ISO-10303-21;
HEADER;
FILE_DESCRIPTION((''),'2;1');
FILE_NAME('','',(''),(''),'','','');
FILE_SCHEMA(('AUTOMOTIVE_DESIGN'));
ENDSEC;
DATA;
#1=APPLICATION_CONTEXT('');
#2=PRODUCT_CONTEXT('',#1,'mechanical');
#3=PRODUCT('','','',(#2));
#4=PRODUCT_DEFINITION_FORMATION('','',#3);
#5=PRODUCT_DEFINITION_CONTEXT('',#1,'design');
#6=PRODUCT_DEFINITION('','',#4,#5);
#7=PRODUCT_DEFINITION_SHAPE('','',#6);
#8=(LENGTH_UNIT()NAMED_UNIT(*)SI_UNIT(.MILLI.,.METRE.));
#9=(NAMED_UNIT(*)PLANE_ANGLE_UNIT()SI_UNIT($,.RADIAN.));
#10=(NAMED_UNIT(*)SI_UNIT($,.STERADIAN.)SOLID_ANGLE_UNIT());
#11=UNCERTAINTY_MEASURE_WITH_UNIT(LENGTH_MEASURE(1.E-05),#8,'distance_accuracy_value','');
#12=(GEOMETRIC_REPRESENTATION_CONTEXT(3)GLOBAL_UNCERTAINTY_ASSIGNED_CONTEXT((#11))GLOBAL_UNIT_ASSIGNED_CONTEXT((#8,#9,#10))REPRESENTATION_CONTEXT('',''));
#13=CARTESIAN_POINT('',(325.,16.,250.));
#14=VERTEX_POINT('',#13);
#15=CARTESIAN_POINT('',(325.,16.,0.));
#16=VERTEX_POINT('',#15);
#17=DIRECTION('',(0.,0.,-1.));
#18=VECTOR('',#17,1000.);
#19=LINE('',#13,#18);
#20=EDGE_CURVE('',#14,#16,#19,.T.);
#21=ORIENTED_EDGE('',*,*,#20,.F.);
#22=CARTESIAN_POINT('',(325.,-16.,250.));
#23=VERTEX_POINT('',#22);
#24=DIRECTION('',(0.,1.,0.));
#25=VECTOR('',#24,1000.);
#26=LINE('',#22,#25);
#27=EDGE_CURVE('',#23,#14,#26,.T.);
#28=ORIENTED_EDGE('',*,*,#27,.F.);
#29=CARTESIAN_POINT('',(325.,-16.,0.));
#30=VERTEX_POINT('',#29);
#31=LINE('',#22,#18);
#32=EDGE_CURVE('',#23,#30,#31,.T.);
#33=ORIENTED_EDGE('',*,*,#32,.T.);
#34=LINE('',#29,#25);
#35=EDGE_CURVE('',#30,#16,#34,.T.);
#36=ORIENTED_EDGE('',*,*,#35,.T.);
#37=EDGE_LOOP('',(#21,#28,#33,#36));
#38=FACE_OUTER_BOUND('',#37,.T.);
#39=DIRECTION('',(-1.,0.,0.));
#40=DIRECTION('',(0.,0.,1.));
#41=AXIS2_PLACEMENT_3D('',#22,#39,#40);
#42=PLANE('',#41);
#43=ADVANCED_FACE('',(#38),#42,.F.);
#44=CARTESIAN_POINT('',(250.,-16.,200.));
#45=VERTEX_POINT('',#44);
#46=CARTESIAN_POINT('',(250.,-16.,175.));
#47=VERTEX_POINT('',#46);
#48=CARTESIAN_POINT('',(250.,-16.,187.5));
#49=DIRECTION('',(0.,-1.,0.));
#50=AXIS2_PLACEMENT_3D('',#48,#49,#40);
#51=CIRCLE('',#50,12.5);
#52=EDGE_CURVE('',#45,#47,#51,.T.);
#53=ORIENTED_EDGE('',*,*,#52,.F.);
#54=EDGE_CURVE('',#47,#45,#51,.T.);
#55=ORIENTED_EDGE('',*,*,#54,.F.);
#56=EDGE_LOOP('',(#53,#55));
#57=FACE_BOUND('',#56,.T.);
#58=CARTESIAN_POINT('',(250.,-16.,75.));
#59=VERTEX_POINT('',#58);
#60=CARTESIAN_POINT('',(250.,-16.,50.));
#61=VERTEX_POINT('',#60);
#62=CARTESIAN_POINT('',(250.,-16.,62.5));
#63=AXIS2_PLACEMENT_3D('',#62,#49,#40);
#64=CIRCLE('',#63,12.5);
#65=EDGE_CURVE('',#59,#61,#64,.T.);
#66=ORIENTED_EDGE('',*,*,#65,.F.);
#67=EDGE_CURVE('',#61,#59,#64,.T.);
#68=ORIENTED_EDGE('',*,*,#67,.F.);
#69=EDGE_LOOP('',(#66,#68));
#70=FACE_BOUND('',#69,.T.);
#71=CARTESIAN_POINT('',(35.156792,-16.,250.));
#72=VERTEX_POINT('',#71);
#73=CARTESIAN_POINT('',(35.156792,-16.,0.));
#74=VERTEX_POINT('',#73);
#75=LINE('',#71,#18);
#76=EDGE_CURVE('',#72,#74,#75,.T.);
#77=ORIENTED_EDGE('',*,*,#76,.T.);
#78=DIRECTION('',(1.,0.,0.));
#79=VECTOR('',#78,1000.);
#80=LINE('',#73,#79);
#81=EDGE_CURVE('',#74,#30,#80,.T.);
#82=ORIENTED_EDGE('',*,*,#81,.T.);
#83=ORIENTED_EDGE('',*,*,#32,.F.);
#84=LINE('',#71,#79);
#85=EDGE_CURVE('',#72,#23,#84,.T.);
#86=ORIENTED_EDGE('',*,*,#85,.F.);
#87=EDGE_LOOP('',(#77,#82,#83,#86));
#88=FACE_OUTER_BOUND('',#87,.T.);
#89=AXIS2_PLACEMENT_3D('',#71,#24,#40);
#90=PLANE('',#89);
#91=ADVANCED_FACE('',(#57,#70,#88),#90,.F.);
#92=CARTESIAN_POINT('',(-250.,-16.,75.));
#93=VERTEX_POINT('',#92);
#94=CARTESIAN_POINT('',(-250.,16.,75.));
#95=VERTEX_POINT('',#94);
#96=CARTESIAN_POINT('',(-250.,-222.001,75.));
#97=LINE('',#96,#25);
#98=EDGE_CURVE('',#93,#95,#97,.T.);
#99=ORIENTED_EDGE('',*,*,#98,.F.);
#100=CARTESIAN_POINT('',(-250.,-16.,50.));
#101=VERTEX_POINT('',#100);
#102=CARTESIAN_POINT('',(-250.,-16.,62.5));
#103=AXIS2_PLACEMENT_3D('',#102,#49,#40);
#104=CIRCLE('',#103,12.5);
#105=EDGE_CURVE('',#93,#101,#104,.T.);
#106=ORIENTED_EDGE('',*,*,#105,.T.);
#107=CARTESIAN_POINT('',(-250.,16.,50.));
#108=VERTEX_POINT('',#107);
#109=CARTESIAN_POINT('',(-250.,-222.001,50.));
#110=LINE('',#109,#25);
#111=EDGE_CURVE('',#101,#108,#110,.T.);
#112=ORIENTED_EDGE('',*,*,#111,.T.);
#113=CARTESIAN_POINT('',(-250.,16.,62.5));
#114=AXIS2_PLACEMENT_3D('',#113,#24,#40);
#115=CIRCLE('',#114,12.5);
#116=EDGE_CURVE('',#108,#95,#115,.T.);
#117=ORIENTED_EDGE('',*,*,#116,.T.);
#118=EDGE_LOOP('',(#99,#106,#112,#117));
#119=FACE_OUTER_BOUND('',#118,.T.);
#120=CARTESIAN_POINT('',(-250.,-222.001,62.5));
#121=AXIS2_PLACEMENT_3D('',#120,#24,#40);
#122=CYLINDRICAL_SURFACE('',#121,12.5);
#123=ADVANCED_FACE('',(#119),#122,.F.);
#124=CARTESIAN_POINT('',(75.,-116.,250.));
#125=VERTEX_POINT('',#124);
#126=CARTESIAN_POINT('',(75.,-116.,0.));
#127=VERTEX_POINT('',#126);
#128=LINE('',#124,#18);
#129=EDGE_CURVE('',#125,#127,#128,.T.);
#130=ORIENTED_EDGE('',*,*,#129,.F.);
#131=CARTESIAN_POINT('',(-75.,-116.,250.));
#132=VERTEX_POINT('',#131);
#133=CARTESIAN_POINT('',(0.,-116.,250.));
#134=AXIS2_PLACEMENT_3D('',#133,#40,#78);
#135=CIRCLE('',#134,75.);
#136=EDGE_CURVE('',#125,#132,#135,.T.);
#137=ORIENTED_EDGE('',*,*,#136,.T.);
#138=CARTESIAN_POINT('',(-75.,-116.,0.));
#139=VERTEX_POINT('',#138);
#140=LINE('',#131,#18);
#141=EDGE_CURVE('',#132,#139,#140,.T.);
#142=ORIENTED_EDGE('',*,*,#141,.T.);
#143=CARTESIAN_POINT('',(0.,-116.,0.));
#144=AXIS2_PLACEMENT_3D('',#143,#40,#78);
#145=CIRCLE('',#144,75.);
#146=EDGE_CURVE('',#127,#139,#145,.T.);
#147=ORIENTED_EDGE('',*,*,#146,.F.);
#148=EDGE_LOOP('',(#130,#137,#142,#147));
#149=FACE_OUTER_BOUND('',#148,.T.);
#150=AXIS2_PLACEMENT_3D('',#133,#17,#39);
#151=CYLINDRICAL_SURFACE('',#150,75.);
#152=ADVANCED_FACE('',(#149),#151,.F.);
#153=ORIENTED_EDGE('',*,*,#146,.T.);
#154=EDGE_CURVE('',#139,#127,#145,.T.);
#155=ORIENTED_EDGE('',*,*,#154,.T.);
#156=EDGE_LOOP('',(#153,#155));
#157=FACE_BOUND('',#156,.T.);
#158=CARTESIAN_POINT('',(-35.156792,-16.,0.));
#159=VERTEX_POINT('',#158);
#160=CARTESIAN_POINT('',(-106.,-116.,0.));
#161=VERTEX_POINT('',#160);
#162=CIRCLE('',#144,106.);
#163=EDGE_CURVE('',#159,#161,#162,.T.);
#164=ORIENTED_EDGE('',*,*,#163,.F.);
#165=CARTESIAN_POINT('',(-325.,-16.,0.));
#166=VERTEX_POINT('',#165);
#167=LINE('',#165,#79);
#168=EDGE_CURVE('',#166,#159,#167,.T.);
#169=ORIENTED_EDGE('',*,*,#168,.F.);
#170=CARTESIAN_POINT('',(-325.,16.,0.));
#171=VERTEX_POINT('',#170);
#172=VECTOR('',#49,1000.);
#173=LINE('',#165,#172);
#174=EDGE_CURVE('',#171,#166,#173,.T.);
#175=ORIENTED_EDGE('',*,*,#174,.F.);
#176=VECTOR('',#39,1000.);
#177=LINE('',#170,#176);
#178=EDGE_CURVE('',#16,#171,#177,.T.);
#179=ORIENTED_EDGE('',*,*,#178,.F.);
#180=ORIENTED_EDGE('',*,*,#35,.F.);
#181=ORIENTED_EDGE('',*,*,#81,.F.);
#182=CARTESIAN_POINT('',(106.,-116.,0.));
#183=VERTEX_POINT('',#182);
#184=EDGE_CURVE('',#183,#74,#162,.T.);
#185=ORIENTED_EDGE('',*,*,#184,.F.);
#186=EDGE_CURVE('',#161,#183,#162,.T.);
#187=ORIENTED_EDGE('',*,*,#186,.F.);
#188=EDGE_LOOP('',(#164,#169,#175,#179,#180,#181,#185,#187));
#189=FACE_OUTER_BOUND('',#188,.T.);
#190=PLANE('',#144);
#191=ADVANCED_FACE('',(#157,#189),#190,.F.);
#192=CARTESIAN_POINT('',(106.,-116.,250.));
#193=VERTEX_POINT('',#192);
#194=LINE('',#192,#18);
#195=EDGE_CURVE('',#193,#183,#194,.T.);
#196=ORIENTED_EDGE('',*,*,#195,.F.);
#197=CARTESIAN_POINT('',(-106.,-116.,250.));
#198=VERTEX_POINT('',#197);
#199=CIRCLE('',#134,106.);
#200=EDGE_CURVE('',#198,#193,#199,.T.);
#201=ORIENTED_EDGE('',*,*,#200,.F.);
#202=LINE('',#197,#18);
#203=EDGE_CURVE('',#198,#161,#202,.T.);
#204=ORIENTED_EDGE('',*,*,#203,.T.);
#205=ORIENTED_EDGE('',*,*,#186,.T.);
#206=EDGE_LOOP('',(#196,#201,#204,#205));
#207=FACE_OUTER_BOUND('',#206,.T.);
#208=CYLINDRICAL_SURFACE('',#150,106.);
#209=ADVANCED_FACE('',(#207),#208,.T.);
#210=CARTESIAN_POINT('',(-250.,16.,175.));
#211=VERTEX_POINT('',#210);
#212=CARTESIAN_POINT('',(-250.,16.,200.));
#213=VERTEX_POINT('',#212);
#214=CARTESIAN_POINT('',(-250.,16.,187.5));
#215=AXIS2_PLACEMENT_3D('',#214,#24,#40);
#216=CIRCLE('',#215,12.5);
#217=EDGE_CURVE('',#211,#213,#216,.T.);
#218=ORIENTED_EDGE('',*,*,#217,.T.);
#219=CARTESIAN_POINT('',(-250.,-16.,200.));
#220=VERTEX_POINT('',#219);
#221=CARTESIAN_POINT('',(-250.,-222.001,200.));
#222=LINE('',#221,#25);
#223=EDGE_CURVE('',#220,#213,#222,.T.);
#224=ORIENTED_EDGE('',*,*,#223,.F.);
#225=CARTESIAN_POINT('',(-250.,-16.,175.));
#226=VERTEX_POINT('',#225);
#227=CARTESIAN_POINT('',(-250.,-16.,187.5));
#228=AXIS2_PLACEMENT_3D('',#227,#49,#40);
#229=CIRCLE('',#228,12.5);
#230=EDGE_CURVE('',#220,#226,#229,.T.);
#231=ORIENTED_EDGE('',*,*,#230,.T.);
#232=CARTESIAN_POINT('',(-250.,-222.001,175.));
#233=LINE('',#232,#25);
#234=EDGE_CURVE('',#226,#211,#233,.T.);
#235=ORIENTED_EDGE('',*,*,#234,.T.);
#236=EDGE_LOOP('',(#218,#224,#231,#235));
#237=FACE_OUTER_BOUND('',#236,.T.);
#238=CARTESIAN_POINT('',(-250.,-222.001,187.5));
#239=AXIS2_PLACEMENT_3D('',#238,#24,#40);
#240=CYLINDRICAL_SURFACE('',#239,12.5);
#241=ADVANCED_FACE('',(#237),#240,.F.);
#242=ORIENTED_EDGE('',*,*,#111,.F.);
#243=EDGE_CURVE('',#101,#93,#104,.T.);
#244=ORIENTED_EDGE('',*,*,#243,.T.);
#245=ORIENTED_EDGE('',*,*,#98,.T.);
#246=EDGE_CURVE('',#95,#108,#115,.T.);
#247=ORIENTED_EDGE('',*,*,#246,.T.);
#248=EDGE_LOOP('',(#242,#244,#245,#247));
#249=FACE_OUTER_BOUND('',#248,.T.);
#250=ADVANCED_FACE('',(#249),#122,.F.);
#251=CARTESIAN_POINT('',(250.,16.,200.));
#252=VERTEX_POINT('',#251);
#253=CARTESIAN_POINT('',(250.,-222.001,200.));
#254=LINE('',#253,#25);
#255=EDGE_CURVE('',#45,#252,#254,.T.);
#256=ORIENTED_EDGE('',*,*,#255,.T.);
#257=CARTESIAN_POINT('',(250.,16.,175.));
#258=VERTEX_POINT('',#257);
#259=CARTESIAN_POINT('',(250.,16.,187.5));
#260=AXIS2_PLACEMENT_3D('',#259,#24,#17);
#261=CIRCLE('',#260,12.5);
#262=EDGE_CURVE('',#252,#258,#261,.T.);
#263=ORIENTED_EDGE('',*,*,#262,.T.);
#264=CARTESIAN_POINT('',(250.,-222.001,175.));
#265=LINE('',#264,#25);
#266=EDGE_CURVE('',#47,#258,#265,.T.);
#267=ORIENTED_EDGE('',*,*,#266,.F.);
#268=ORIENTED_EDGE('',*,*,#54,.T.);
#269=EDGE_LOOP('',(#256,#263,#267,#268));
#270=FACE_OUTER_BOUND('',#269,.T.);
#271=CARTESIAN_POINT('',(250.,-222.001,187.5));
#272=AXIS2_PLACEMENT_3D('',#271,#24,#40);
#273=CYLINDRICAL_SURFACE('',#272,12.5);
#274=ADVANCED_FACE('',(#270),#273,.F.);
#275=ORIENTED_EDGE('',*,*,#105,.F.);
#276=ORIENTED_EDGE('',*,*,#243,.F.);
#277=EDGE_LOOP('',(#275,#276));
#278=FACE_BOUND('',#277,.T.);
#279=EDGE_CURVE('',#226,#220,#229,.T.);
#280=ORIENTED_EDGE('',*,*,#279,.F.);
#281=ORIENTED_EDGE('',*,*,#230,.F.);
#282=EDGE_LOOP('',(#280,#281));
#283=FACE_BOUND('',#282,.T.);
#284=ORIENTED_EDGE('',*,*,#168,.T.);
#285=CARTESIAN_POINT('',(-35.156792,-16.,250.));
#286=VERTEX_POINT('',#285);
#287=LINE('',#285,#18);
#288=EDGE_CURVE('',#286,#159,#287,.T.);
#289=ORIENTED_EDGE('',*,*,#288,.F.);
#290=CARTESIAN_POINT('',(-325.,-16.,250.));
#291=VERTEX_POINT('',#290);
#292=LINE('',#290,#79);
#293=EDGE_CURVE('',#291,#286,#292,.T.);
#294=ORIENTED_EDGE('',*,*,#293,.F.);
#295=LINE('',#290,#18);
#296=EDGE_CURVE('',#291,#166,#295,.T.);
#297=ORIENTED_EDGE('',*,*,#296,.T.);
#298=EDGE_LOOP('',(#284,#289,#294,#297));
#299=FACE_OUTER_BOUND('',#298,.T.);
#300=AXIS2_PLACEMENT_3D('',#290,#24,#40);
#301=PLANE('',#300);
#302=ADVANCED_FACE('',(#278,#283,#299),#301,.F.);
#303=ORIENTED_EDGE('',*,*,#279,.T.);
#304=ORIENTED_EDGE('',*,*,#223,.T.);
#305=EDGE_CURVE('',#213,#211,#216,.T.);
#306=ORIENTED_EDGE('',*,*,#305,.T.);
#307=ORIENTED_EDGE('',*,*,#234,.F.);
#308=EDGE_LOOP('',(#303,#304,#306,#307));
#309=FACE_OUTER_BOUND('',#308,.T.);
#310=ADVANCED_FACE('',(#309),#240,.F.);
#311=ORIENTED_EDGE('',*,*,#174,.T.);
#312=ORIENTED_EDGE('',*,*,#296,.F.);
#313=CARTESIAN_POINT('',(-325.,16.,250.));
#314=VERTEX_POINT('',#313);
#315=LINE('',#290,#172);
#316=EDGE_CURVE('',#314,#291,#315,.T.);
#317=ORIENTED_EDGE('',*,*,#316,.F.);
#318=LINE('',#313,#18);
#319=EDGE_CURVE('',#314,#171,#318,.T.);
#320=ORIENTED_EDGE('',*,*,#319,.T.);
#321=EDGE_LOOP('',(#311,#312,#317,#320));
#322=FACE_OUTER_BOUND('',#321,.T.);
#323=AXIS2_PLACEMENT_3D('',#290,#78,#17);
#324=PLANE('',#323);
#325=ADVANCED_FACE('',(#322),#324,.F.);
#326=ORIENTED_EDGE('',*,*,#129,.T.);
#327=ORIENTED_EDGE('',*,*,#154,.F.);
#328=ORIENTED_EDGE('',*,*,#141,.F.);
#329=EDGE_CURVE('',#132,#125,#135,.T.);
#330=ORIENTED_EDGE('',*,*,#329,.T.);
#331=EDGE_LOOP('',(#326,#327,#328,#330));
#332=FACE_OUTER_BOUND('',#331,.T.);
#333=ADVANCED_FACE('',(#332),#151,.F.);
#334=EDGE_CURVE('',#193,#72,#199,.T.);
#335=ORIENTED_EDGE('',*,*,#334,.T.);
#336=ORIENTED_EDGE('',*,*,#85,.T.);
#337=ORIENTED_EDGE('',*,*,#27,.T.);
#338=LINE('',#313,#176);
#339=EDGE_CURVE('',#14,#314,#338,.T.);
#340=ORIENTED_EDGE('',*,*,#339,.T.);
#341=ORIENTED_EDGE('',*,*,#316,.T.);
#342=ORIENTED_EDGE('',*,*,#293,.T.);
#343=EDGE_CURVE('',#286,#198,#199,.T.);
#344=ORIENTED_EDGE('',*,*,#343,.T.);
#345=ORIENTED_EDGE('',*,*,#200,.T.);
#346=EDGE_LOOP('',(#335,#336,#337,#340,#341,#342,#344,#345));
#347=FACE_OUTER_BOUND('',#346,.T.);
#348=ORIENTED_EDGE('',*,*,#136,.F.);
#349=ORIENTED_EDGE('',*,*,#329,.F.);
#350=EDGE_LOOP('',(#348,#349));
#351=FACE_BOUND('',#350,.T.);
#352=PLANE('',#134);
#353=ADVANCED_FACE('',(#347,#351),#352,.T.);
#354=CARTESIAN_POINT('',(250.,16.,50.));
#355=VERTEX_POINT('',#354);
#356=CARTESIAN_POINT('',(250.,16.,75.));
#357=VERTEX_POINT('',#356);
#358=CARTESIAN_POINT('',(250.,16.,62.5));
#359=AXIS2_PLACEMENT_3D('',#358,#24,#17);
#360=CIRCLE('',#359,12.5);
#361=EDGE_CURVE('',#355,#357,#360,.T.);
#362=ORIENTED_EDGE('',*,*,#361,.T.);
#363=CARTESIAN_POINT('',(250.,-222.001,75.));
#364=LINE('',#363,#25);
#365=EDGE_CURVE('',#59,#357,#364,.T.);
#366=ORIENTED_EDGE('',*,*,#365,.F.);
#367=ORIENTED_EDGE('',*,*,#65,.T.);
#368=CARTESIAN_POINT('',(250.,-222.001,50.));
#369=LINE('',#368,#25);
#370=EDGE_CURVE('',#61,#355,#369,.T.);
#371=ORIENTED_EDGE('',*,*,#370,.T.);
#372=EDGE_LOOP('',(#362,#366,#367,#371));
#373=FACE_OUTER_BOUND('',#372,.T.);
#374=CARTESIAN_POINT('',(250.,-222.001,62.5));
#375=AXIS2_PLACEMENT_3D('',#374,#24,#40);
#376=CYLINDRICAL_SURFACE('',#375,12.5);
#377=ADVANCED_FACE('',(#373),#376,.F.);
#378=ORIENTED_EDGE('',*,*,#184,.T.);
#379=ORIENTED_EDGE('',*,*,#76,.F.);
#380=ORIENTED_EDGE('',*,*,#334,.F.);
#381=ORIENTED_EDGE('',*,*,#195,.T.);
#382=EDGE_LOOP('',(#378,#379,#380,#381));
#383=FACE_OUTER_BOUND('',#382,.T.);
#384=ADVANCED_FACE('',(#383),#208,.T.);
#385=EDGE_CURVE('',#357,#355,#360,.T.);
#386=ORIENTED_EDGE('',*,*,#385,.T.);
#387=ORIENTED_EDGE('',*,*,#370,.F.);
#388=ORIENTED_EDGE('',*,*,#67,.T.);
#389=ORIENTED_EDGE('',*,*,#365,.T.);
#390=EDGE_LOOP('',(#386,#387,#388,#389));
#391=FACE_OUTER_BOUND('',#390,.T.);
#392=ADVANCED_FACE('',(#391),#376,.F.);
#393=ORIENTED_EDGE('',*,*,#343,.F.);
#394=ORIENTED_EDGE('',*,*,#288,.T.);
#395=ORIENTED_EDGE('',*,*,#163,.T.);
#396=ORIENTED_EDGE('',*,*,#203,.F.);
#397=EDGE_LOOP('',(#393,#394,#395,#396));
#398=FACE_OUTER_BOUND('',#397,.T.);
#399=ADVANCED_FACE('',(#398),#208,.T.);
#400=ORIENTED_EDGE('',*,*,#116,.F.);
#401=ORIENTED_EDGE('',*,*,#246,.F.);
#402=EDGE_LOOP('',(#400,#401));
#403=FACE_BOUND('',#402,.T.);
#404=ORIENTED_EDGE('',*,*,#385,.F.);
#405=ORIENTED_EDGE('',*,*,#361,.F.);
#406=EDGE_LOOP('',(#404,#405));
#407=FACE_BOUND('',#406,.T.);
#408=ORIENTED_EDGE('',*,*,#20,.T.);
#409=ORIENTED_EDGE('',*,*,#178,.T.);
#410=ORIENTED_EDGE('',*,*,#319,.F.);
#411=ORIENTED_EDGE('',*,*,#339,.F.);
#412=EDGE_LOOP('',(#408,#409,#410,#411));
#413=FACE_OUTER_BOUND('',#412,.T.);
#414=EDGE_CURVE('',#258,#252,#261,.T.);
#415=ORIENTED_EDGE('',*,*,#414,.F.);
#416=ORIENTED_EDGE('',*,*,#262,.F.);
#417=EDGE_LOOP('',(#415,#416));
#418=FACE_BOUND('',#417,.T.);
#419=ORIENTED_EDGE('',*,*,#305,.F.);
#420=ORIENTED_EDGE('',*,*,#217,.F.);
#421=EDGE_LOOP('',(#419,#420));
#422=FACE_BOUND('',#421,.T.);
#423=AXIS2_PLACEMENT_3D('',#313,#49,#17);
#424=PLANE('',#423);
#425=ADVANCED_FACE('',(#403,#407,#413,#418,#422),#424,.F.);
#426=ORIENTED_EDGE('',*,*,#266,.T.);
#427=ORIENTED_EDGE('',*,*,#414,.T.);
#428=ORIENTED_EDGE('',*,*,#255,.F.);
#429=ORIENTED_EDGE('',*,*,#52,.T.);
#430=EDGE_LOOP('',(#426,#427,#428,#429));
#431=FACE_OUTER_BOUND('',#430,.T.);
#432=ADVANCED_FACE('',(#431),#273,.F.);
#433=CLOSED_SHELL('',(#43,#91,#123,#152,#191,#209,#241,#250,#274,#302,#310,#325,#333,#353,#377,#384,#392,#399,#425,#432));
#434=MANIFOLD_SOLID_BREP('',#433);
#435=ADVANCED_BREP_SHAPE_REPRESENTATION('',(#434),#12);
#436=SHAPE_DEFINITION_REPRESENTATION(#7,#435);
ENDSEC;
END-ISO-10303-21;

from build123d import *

# Parameters (mm, degrees)
PLATE_AND_TUBE_PROFILE_SKETCH_R = 75
PLATE_AND_TUBE_BODY_DEPTH       = 250
MOUNTING_HOLES_4X_REACH         = 476.098
MOUNTING_HOLES_SKETCH_R         = 12.5


with BuildPart() as part:
    # Plate and Tube Profile Sketch → Plate and Tube Body (new body)
    with BuildSketch(Plane.XY):
        with BuildLine():
            Line((35.156791662, -16), (325, -16))
            Line((325, -16), (325, 16))
            Line((325, 16), (-325, 16))
            Line((-325, 16), (-325, -16))
            Line((-325, -16), (-35.156791662, -16))
            ThreePointArc((-35.156791662, -16), (0, -222), (35.156791662, -16))
        make_face()
        with Locations((0, -116)):
            Circle(PLATE_AND_TUBE_PROFILE_SKETCH_R, mode=Mode.SUBTRACT)
    extrude(amount=PLATE_AND_TUBE_BODY_DEPTH)

    # Mounting Holes Sketch → Mounting Holes 4x (cut, up to next)
    with BuildSketch(Plane(origin=(0, 16, 0), x_dir=(1, 0, 0), z_dir=(0, 1, 0)), mode=Mode.PRIVATE) as mounting_holes_4x_sk1:
        with Locations(Location((-250, -62.5, 0), (0, 0, 270))):
            Circle(MOUNTING_HOLES_SKETCH_R)
    mounting_holes_4x_tool1 = extrude(mounting_holes_4x_sk1.sketch, amount=-MOUNTING_HOLES_4X_REACH, mode=Mode.PRIVATE) & part.part
    # Mounting Holes Sketch → Mounting Holes 4x (cut, up to next)
    with BuildSketch(Plane(origin=(0, 16, 0), x_dir=(1, 0, 0), z_dir=(0, 1, 0)), mode=Mode.PRIVATE) as mounting_holes_4x_sk2:
        with Locations(Location((250, -62.5, 0), (0, 0, 270))):
            Circle(MOUNTING_HOLES_SKETCH_R)
    mounting_holes_4x_tool2 = extrude(mounting_holes_4x_sk2.sketch, amount=-MOUNTING_HOLES_4X_REACH, mode=Mode.PRIVATE) & part.part
    # Mounting Holes Sketch → Mounting Holes 4x (cut, up to next)
    with BuildSketch(Plane(origin=(0, 16, 0), x_dir=(1, 0, 0), z_dir=(0, 1, 0)), mode=Mode.PRIVATE) as mounting_holes_4x_sk3:
        with Locations(Location((-250, -187.5, 0), (0, 0, 270))):
            Circle(MOUNTING_HOLES_SKETCH_R)
    mounting_holes_4x_tool3 = extrude(mounting_holes_4x_sk3.sketch, amount=-MOUNTING_HOLES_4X_REACH, mode=Mode.PRIVATE) & part.part
    # Mounting Holes Sketch → Mounting Holes 4x (cut, up to next)
    with BuildSketch(Plane(origin=(0, 16, 0), x_dir=(1, 0, 0), z_dir=(0, 1, 0)), mode=Mode.PRIVATE) as mounting_holes_4x_sk4:
        with Locations(Location((250, -187.5, 0), (0, 0, 270))):
            Circle(MOUNTING_HOLES_SKETCH_R)
    mounting_holes_4x_tool4 = extrude(mounting_holes_4x_sk4.sketch, amount=-MOUNTING_HOLES_4X_REACH, mode=Mode.PRIVATE) & part.part
    add(mounting_holes_4x_tool1.solids().sort_by_distance((-250, 16, 62.5))[0], mode=Mode.SUBTRACT)
    add(mounting_holes_4x_tool2.solids().sort_by_distance((250, 16, 62.5))[0], mode=Mode.SUBTRACT)
    add(mounting_holes_4x_tool3.solids().sort_by_distance((-250, 16, 187.5))[0], mode=Mode.SUBTRACT)
    add(mounting_holes_4x_tool4.solids().sort_by_distance((250, 16, 187.5))[0], mode=Mode.SUBTRACT)


solid = part.part
